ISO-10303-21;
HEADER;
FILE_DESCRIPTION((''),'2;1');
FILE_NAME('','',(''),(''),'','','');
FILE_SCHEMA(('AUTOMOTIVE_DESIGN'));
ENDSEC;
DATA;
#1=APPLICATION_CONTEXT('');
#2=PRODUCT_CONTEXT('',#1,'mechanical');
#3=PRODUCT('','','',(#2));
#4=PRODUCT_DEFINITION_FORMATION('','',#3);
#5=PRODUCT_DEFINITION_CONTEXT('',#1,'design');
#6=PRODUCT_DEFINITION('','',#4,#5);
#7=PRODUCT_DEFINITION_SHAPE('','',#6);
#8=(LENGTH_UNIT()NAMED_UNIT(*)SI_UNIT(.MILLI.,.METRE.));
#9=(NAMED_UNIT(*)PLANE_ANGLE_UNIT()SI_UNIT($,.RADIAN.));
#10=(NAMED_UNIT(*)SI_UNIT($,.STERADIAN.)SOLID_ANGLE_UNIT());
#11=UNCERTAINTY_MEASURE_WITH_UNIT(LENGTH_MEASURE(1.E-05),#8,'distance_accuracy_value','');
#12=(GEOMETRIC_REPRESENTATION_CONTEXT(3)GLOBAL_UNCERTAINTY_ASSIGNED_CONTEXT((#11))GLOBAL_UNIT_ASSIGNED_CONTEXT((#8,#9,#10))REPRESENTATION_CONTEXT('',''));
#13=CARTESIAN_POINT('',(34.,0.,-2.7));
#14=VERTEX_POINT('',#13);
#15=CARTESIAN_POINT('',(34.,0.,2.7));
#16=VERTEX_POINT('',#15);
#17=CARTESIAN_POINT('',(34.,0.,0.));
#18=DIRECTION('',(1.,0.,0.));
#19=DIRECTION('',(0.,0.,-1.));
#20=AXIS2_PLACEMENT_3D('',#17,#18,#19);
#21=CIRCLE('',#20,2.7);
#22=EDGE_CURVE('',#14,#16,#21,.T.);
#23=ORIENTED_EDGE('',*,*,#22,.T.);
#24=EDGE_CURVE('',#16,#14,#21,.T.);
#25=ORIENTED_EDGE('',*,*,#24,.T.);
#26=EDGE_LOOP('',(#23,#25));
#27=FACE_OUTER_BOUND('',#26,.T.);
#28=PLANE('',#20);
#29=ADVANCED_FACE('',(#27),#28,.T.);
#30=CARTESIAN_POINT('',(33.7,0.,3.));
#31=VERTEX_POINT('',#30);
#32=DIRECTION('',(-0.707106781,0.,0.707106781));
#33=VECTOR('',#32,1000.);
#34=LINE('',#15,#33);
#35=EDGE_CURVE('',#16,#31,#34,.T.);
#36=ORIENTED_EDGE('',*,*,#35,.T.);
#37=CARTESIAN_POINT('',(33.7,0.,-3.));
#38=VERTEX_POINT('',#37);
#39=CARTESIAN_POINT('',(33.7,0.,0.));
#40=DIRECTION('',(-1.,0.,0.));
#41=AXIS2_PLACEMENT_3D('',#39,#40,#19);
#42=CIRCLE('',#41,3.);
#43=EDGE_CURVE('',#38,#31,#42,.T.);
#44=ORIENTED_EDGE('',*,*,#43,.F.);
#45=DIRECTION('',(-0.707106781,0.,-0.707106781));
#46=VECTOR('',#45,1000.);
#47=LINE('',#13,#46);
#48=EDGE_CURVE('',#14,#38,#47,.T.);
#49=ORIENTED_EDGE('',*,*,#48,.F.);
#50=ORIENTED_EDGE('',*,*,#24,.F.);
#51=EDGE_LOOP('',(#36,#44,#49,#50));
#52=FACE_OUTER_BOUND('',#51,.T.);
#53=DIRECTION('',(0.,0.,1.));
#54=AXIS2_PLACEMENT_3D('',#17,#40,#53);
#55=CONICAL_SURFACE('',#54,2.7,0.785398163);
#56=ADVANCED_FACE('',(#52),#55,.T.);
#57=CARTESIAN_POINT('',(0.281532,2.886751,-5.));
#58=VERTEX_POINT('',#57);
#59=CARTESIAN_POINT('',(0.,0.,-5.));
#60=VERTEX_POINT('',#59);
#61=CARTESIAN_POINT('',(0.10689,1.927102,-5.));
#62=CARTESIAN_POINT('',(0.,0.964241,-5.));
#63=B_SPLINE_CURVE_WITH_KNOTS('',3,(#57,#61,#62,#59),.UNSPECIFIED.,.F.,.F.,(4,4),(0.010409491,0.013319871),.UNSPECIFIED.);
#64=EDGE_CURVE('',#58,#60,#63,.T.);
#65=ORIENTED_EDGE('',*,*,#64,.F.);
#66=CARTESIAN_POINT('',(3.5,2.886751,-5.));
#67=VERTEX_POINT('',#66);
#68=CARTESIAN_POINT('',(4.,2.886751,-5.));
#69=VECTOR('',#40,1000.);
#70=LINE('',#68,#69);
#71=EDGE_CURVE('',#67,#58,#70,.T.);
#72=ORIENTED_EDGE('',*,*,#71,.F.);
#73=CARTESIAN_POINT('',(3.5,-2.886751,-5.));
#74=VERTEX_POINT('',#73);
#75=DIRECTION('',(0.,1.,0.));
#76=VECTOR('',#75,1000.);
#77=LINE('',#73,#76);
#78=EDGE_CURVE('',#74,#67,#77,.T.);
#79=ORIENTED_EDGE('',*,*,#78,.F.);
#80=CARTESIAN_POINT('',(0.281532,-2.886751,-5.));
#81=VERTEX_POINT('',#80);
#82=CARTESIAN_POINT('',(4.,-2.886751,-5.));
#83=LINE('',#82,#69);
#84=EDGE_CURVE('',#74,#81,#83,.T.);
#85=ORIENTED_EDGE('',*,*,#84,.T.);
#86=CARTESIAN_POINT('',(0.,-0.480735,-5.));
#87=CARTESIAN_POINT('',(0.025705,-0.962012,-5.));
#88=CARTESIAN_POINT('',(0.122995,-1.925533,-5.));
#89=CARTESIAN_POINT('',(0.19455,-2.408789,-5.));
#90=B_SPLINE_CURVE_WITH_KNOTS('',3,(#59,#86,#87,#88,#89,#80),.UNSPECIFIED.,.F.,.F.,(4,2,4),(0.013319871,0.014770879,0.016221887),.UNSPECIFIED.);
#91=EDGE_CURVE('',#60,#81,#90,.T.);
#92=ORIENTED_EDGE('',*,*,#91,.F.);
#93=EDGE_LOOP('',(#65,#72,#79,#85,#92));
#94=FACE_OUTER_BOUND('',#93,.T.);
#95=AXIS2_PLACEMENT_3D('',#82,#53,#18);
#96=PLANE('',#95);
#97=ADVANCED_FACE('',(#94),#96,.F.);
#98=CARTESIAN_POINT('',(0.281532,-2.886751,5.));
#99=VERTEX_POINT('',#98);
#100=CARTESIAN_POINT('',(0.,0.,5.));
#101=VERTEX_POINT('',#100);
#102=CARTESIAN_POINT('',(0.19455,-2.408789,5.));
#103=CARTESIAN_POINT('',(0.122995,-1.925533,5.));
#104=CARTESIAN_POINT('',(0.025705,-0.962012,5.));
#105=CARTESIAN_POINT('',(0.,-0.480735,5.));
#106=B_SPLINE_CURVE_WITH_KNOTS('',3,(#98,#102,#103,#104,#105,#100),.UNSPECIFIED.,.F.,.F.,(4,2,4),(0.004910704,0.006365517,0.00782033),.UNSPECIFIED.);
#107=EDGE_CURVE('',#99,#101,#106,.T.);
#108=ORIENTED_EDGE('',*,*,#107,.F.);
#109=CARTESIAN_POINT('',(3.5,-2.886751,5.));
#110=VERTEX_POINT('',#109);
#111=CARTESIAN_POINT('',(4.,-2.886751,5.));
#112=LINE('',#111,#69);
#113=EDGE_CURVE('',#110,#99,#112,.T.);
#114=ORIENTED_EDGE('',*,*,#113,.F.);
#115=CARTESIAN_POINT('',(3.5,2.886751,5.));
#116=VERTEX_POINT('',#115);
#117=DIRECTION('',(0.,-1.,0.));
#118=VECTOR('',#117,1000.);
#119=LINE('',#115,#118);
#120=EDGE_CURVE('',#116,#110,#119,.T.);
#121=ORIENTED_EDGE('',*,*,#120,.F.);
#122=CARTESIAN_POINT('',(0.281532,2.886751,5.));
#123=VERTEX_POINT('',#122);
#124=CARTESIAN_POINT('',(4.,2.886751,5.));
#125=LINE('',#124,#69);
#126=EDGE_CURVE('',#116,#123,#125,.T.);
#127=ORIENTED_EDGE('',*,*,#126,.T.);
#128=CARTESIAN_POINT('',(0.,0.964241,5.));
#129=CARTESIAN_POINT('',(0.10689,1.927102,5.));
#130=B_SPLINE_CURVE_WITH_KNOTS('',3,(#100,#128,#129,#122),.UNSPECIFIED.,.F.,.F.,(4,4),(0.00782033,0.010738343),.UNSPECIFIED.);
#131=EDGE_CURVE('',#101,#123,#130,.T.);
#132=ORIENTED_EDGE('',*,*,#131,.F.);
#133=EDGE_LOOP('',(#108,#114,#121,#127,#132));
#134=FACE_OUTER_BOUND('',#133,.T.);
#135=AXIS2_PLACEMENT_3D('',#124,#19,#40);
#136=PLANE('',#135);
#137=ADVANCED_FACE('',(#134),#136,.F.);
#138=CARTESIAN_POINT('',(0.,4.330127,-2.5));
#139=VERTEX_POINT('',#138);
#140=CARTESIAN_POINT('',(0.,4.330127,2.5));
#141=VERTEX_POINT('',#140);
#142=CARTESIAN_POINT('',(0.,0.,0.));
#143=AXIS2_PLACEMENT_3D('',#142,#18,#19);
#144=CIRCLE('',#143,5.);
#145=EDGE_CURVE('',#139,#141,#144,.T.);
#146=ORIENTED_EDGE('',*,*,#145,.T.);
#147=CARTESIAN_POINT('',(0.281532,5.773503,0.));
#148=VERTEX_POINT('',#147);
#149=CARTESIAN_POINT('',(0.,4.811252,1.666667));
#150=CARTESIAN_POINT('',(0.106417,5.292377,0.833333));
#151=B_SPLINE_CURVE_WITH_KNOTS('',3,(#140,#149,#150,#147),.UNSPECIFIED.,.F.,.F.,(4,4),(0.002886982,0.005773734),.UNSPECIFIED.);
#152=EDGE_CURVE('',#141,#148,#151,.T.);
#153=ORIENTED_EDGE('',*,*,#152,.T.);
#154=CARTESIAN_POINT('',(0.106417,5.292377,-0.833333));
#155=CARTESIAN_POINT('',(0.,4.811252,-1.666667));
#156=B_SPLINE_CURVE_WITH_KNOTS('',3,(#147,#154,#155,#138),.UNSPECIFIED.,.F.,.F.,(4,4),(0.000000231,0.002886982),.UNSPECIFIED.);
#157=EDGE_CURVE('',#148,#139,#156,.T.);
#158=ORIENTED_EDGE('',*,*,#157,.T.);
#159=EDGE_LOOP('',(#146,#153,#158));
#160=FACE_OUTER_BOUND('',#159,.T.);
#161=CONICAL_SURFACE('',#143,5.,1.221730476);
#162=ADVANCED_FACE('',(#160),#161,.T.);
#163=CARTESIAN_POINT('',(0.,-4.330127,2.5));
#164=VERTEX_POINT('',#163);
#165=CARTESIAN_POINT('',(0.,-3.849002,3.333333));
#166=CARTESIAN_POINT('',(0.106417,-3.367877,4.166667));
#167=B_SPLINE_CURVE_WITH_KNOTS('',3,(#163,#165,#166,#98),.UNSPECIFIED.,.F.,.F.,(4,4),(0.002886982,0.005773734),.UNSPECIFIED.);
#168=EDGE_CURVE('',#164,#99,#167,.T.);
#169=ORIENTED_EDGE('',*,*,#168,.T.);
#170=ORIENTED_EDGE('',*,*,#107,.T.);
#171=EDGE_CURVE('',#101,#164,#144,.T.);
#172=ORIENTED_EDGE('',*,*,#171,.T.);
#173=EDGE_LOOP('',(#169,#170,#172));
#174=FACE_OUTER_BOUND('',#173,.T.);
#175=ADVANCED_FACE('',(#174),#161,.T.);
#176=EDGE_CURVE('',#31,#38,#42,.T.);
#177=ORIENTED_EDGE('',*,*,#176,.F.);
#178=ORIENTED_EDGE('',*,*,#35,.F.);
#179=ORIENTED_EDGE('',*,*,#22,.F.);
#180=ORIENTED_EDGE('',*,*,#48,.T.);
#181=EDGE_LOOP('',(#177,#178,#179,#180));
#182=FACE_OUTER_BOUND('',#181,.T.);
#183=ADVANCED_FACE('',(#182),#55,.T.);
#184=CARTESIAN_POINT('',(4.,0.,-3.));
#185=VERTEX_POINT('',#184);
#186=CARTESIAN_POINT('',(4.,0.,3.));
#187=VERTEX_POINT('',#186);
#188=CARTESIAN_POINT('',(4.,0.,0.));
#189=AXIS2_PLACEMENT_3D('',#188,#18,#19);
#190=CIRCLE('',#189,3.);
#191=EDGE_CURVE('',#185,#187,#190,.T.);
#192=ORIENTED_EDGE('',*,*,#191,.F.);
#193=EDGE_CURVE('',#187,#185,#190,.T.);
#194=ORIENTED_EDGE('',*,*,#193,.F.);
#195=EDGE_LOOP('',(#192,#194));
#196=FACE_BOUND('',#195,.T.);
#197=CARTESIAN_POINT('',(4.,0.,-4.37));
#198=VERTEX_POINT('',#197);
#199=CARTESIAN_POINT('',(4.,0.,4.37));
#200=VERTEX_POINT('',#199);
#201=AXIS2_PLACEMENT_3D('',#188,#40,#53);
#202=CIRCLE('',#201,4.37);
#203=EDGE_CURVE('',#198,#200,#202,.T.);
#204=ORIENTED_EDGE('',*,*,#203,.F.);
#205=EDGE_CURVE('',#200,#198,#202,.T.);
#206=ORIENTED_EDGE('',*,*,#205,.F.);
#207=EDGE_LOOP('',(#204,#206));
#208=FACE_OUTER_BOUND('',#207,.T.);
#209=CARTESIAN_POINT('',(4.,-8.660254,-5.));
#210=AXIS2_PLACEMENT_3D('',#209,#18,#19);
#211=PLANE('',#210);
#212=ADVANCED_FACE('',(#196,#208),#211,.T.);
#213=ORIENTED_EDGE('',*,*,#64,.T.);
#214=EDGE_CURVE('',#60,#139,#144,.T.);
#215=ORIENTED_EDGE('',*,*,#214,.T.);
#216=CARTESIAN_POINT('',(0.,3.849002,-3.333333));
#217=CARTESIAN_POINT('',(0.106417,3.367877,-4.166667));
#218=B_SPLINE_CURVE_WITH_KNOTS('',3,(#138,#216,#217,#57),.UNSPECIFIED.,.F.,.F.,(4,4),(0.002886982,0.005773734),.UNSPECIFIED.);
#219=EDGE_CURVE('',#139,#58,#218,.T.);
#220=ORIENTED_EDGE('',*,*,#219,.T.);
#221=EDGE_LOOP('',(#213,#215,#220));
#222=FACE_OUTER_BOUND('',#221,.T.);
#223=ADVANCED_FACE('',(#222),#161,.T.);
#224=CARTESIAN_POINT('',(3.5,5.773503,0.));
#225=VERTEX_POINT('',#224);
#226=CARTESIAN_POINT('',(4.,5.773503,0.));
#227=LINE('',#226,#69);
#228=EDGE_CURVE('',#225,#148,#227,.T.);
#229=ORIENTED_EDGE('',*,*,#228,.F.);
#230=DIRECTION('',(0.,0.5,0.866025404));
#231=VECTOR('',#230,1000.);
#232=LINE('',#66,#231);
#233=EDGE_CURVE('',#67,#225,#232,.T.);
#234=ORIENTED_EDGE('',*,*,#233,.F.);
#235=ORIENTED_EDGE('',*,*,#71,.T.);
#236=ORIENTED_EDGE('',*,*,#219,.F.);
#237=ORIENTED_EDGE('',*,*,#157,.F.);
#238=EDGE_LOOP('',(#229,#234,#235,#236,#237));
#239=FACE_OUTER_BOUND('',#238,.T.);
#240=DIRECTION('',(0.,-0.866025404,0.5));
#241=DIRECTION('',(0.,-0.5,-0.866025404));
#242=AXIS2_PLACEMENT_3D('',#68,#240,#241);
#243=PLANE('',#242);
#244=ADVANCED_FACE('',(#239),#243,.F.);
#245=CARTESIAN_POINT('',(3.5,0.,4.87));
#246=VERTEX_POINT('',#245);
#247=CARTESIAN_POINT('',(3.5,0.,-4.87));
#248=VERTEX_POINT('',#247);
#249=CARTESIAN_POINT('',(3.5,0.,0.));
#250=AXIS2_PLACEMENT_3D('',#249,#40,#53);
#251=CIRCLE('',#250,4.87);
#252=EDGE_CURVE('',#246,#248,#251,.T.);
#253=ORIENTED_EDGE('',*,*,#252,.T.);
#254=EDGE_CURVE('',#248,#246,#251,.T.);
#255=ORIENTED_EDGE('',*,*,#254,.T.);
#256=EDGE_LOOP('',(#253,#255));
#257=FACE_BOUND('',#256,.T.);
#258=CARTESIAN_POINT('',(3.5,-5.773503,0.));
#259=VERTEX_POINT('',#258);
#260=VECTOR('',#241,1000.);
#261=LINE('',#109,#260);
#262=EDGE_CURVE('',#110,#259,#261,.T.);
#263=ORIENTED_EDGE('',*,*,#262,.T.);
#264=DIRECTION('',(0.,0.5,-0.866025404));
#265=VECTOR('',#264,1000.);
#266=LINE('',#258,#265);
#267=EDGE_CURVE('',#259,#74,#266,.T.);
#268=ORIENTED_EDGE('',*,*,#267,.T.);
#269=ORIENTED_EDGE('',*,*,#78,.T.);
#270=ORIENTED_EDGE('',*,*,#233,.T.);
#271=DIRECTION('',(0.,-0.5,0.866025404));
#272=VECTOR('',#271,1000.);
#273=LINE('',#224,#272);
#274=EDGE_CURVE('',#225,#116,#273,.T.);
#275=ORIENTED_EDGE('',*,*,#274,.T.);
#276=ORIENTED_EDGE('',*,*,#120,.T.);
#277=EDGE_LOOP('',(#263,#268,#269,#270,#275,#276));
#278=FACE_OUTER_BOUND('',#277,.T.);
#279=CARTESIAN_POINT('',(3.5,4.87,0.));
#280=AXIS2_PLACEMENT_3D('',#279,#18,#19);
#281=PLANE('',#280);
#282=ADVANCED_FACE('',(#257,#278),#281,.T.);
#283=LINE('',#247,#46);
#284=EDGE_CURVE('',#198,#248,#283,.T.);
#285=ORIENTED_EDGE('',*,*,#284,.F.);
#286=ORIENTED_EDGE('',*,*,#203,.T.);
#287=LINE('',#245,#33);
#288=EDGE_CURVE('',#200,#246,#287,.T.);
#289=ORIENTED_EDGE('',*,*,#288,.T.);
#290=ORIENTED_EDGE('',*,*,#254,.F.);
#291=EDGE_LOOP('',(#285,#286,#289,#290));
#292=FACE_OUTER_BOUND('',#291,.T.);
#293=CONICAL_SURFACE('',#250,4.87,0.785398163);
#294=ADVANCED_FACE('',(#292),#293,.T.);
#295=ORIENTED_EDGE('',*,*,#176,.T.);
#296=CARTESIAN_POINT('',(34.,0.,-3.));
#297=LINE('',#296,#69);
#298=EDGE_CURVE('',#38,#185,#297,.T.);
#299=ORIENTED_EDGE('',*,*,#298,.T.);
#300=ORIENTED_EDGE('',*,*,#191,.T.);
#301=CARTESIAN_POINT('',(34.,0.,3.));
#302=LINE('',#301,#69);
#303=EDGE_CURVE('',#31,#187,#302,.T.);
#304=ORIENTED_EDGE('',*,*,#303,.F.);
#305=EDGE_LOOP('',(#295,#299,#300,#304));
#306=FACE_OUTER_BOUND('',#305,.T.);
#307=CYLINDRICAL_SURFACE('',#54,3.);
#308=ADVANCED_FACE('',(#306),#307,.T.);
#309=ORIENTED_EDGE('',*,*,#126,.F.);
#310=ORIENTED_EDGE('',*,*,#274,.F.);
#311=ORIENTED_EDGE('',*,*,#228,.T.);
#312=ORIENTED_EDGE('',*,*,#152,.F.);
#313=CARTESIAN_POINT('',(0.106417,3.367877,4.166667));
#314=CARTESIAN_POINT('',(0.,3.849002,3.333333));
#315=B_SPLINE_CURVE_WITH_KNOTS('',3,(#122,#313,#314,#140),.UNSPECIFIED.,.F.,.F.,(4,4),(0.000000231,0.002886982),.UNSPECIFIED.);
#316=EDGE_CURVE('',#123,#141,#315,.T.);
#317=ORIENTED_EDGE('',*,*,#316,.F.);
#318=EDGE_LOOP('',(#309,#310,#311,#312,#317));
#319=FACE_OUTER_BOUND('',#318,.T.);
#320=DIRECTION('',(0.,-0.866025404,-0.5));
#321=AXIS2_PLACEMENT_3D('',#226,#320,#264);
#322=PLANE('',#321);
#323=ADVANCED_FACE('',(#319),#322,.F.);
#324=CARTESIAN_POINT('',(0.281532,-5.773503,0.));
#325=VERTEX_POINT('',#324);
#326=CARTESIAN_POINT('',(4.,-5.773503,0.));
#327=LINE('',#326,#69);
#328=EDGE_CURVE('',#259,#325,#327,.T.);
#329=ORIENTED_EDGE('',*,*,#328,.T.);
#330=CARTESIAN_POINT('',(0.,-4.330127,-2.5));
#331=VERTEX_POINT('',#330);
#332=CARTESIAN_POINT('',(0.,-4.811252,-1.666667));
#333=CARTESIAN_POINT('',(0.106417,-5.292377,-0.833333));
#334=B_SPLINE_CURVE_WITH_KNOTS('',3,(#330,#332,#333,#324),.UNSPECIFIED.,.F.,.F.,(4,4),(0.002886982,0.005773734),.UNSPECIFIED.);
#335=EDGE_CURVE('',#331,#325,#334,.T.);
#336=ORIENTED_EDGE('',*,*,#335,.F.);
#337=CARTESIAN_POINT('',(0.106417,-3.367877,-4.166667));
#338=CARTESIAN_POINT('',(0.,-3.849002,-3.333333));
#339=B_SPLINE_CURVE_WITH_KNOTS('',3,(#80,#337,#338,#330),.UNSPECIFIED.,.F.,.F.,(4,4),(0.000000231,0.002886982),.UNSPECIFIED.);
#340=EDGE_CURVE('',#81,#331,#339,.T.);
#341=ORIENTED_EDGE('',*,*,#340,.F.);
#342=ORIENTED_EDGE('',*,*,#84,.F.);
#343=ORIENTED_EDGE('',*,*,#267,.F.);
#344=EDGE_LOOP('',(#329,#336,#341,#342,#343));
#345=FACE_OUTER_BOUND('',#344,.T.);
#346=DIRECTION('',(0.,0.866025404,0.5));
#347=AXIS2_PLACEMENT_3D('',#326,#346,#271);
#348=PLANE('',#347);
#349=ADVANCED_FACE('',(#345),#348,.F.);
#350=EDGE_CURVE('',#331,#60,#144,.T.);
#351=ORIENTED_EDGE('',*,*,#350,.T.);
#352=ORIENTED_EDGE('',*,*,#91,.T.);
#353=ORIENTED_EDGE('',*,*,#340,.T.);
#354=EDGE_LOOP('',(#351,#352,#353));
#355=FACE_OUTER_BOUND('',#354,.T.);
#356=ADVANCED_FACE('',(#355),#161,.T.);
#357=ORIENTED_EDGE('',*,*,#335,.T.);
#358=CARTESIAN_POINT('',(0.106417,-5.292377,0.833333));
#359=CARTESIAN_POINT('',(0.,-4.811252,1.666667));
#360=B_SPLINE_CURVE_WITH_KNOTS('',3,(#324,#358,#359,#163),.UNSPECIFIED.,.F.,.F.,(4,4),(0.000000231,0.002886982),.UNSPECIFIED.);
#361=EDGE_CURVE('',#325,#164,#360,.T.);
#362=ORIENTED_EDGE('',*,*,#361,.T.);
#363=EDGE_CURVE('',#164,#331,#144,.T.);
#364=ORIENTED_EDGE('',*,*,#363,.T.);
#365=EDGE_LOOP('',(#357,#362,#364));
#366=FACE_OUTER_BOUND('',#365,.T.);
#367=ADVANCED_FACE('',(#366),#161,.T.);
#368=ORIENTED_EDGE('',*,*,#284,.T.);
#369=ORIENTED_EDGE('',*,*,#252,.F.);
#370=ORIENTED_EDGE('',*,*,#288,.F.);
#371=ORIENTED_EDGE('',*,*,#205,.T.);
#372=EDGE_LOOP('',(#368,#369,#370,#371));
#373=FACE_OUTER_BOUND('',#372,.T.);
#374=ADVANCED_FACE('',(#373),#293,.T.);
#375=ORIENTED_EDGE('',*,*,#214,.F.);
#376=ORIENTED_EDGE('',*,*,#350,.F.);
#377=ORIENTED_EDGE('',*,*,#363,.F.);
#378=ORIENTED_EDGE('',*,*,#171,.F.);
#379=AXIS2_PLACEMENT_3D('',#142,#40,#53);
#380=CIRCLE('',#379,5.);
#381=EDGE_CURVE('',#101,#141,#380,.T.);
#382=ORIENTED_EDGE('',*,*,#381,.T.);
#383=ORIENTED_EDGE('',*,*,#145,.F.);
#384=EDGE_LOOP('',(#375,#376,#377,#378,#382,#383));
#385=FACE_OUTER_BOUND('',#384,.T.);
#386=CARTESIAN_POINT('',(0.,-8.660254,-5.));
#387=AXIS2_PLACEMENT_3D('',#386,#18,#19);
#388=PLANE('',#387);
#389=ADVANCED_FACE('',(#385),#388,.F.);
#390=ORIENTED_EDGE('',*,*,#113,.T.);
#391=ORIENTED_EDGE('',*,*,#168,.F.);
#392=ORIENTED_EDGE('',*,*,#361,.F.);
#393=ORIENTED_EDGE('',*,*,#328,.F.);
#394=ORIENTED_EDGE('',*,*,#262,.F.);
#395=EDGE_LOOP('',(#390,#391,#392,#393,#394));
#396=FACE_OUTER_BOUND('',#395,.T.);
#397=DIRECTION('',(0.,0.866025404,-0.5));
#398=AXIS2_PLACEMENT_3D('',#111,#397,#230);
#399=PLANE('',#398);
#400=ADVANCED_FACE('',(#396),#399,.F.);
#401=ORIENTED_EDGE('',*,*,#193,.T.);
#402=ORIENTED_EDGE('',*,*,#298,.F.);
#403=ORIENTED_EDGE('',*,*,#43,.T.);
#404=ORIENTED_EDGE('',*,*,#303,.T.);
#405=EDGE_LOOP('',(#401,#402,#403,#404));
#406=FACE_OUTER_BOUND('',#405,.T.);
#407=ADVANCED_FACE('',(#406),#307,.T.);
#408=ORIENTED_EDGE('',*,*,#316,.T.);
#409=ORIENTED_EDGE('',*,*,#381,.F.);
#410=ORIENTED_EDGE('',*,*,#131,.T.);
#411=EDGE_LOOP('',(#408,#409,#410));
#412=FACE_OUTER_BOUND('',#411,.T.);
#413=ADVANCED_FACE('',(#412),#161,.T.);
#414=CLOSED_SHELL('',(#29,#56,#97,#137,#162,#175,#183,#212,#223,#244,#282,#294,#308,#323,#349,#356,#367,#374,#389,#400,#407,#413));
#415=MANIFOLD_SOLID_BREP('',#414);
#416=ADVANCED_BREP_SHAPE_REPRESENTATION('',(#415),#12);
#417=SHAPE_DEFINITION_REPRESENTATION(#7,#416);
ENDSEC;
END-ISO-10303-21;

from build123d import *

# Parameters (mm, degrees)
BASEHEAD_DEPTH = 4
SKETCH5_R      = 3
BASEBODY_DEPTH = 30
CHAMFER1_SIZE  = 0.3


with BuildPart() as part:
    # Sketch2 → BaseHead (new body)
    with BuildSketch(Plane(origin=(0, 0, 0), x_dir=(0, 0, -1), z_dir=(1, 0, 0))):
        Polygon((0, -5.773502692), (5, -2.886751346), (5, 2.886751346), (0, 5.773502692), (-5, 2.886751346), (-5, -2.886751346), align=None)
    extrude(amount=BASEHEAD_DEPTH)

    # Sketch3 → BearingFace (revolve, cut)
    with BuildSketch(Plane.XY, mode=Mode.PRIVATE) as bearingface_sk:
        Polygon((4, 5.773502692), (4, 4.37), (3.5, 4.87), (3.5, 5.773502692), align=None)
    revolve(bearingface_sk.sketch.rotate(Axis((-0.957090588, 0, 0), (1, 0, 0)), 90), axis=Axis((-0.957090588, 0, 0), (1, 0, 0)), mode=Mode.SUBTRACT)

    # Sketch4 → HeadChamfer (revolve, cut)
    with BuildSketch(Plane.XY):
        Polygon((0, 5.773502692), (0.281531956, 5.773502692), (0, 5), align=None)
    revolve(axis=Axis((-0.493528746, 0, 0), (1, 0, 0)), mode=Mode.SUBTRACT)

    # Sketch5 → BaseBody (add)
    with BuildSketch(Plane(origin=(4, 0, 0), x_dir=(0, 0, -1), z_dir=(1, 0, 0))):
        Circle(SKETCH5_R)
    extrude(amount=BASEBODY_DEPTH)

    # Chamfer1
    chamfer1_edges = [part.edges().sort_by_distance(p)[0] for p in [
        (34, 0, 3),
    ]]
    chamfer(chamfer1_edges, length=CHAMFER1_SIZE)


solid = part.part
